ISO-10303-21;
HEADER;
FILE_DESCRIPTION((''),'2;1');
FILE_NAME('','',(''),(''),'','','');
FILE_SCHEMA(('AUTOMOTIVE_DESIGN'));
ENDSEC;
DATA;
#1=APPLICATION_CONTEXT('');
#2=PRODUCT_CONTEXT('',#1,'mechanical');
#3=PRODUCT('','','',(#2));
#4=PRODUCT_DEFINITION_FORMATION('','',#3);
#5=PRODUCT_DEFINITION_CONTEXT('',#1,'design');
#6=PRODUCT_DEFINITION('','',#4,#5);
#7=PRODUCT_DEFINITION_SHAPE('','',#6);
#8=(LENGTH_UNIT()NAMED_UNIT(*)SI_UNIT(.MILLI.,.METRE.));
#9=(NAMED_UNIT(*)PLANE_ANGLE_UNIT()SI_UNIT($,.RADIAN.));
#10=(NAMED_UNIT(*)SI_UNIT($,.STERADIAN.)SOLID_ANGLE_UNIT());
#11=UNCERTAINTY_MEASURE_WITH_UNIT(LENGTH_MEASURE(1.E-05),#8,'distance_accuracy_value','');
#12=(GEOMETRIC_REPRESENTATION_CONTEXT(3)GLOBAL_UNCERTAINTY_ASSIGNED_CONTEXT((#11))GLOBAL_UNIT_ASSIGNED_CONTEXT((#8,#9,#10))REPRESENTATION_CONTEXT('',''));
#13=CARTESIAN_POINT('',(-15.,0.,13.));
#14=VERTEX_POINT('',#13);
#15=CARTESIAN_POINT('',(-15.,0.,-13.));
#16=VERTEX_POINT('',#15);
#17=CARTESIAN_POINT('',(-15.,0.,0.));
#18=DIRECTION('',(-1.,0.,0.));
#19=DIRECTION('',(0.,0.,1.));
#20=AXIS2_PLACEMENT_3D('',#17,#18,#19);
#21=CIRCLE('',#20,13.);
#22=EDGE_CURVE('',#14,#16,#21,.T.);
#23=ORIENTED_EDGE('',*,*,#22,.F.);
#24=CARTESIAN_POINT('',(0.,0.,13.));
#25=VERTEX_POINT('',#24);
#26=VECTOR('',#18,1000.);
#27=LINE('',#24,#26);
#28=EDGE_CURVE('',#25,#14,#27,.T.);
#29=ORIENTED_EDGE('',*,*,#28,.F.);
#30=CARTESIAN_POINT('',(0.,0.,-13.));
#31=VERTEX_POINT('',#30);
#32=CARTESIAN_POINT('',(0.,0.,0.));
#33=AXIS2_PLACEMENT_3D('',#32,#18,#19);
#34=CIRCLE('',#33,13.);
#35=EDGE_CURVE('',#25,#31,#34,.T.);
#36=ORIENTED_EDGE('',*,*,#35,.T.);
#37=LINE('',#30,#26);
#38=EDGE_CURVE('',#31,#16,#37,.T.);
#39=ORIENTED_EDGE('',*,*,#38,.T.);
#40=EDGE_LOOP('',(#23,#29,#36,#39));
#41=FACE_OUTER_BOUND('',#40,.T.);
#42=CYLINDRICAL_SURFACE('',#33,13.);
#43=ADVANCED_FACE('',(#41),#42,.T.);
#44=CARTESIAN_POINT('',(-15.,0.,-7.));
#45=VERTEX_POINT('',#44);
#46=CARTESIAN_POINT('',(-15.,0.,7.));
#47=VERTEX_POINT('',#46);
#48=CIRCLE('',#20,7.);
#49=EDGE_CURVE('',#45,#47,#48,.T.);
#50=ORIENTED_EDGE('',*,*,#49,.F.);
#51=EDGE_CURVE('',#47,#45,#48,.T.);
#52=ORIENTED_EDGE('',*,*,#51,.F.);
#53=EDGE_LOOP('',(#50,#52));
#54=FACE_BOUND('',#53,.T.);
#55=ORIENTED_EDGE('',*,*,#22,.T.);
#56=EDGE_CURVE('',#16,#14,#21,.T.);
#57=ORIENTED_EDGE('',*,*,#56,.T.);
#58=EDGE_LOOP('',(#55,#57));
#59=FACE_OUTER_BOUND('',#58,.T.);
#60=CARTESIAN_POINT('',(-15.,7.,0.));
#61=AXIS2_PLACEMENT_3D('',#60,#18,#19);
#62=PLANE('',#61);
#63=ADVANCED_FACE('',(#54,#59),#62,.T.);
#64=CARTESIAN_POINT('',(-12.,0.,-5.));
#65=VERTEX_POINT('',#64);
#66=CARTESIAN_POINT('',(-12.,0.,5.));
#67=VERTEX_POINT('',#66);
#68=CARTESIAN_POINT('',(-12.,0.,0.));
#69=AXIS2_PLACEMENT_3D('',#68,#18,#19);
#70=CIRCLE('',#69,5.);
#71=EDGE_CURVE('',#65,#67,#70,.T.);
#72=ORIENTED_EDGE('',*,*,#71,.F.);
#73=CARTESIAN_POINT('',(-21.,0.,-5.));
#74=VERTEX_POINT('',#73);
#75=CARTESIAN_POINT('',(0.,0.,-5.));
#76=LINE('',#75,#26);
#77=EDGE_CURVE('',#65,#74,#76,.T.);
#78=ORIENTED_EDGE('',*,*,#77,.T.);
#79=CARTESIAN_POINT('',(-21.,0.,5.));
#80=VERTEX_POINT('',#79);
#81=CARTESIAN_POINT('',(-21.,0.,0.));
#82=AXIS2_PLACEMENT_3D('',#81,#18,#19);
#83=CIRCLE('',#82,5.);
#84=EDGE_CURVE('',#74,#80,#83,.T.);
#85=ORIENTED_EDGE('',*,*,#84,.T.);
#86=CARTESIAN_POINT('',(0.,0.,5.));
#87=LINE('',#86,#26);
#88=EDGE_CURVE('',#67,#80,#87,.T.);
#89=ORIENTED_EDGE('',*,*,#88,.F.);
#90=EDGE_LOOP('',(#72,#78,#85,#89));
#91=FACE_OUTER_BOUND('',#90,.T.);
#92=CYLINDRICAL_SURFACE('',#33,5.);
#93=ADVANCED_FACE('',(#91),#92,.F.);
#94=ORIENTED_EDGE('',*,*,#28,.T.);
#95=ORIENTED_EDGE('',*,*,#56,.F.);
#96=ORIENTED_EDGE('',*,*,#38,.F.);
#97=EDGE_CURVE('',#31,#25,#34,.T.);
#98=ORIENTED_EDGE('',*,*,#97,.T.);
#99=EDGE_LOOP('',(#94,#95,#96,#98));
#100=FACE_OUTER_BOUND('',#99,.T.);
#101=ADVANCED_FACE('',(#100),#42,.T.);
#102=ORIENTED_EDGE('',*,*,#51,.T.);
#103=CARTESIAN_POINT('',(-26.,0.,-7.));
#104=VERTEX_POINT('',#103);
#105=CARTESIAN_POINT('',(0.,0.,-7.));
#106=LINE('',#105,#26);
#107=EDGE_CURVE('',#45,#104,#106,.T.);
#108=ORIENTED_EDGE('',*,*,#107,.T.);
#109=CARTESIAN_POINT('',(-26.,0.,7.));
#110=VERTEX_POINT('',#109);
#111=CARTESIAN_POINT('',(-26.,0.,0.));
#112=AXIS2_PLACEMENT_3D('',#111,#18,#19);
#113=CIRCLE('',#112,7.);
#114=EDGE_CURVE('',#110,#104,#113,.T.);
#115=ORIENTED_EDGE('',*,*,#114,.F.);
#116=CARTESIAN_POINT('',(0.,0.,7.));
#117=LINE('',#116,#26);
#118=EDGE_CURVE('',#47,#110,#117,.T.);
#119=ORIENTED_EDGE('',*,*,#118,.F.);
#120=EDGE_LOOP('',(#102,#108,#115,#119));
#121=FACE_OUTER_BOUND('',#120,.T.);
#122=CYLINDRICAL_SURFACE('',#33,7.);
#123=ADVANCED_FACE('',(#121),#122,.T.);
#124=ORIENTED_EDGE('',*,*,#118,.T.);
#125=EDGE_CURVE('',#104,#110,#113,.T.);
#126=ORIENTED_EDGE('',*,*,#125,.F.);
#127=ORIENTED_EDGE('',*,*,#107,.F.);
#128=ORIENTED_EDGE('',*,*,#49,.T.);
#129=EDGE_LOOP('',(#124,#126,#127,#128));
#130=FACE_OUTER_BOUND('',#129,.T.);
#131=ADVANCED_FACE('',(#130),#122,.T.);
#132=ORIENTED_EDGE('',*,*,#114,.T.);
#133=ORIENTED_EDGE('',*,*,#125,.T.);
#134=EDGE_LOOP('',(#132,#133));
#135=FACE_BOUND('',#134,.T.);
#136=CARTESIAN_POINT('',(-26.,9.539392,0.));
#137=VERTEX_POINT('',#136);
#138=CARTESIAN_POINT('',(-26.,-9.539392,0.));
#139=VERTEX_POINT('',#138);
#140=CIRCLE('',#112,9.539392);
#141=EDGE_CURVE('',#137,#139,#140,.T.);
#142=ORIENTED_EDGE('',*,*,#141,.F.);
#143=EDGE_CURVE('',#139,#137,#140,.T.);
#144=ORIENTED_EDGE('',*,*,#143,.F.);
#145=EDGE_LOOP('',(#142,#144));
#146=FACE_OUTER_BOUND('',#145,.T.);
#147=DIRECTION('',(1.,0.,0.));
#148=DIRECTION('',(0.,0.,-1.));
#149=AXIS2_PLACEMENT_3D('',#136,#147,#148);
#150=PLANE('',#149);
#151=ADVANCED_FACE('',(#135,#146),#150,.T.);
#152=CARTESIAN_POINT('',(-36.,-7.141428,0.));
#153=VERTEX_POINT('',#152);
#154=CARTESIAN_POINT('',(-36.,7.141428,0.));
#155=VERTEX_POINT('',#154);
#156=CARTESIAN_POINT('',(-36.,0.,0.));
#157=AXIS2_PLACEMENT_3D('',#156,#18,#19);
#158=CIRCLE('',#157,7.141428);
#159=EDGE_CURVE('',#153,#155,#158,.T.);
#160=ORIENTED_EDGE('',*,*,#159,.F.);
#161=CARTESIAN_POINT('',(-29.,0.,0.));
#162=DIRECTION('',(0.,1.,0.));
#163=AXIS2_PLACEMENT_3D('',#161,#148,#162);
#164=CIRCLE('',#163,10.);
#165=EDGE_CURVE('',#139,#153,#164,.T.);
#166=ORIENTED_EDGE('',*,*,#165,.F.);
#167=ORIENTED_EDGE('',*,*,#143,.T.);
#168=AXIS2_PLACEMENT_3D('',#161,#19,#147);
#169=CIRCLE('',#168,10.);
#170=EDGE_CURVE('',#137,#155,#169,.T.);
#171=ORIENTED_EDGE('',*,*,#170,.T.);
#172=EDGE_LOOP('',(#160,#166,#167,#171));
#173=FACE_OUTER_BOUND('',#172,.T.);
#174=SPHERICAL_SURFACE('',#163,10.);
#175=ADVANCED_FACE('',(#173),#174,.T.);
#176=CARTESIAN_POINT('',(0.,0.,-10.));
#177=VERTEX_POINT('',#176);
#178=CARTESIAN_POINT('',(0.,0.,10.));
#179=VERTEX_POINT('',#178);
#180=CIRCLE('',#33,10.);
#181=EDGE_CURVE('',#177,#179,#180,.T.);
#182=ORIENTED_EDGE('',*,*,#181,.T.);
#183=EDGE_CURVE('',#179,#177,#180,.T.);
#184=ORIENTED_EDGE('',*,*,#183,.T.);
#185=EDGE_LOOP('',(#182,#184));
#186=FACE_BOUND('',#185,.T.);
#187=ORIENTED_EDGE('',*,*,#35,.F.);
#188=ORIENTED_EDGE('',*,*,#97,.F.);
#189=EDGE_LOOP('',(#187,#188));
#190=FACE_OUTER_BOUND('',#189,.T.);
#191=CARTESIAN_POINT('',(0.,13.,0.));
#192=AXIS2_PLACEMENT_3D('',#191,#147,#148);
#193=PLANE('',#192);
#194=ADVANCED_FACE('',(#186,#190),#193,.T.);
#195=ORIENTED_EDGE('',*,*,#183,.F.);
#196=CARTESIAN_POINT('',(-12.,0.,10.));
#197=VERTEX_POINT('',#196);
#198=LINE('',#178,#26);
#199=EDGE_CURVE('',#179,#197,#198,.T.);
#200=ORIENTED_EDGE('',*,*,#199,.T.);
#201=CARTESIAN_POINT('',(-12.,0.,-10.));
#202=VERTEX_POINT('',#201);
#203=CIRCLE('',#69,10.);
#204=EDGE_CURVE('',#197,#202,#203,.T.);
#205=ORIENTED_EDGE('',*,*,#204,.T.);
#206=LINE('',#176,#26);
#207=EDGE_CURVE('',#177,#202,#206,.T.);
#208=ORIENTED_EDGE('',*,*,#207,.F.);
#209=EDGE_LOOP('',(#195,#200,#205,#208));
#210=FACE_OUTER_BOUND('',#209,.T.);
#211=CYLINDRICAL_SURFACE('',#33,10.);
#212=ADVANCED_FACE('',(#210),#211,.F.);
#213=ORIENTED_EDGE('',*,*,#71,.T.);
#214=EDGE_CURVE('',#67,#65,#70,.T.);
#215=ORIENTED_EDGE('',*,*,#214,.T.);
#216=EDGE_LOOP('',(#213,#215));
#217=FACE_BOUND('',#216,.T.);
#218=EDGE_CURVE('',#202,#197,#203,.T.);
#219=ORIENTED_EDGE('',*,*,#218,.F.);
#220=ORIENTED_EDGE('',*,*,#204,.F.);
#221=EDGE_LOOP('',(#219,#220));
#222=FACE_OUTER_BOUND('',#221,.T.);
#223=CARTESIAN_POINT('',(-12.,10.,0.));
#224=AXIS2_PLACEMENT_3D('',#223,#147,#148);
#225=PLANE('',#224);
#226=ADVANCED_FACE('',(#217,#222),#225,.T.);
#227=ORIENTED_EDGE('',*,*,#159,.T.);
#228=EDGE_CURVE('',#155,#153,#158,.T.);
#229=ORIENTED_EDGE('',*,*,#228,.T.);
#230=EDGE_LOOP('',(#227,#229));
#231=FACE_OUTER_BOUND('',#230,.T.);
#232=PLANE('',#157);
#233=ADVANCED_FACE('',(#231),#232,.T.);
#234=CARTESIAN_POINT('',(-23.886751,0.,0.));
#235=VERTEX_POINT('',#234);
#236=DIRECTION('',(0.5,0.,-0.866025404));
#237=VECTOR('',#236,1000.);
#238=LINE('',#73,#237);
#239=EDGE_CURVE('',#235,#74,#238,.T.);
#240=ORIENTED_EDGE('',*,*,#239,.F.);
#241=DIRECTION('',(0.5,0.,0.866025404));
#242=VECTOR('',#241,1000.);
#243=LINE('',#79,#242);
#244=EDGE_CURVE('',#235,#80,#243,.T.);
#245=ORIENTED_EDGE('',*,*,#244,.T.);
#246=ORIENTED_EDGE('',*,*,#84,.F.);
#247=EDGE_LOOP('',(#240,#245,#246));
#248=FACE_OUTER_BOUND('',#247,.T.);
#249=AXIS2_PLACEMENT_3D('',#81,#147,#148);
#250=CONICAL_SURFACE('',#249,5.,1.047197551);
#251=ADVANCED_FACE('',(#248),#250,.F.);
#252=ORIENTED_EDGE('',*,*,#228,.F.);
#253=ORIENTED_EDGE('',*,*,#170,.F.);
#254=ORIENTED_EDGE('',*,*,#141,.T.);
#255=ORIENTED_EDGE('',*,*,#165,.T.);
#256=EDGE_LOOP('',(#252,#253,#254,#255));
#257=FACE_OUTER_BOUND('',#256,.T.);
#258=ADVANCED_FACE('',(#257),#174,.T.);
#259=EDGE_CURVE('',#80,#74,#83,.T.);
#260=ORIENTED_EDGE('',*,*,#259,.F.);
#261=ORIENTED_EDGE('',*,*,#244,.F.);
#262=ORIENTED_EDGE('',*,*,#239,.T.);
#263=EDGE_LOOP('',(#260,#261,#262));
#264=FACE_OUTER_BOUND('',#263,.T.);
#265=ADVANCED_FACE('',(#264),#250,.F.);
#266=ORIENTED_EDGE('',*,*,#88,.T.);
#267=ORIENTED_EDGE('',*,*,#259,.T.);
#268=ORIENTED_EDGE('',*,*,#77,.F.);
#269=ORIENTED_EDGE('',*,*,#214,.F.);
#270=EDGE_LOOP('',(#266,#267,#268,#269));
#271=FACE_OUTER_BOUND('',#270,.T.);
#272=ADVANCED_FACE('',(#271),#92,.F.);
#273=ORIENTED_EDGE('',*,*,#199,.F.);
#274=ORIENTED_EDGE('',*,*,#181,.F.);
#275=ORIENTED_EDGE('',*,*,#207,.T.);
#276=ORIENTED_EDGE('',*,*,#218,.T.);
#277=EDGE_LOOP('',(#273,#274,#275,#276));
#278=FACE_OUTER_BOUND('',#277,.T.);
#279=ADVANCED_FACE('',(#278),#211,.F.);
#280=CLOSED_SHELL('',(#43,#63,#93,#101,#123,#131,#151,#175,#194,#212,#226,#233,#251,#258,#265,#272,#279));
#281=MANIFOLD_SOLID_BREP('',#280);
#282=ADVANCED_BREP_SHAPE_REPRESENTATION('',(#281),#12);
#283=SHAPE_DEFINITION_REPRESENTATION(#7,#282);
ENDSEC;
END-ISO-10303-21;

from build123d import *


with BuildPart() as part:
    # Sketch1 → Revolve1 (revolve)
    with BuildSketch(Plane(origin=(0, 0, 0), x_dir=(-1, 0, 0), z_dir=(0, 0, -1)), mode=Mode.PRIVATE) as revolve1_sk:
        with BuildLine():
            Line((21, 5), (23.886751346, 0))
            Line((23.886751346, 0), (36, 0))
            Line((36, 0), (36, 7.141428429))
            ThreePointArc((36, 7.141428429), (31.331857058, 9.724322221), (26, 9.539392014))
            Line((26, 9.539392014), (26, 7))
            Line((26, 7), (15, 7))
            Line((15, 7), (15, 13))
            Line((15, 13), (0, 13))
            Line((0, 13), (0, 10))
            Line((0, 10), (12, 10))
            Line((12, 10), (12, 5))
            Line((12, 5), (21, 5))
        make_face()
    revolve(revolve1_sk.sketch.rotate(Axis((0, 0, 0), (-1, 0, 0)), 270), axis=Axis((0, 0, 0), (-1, 0, 0)))


solid = part.part
